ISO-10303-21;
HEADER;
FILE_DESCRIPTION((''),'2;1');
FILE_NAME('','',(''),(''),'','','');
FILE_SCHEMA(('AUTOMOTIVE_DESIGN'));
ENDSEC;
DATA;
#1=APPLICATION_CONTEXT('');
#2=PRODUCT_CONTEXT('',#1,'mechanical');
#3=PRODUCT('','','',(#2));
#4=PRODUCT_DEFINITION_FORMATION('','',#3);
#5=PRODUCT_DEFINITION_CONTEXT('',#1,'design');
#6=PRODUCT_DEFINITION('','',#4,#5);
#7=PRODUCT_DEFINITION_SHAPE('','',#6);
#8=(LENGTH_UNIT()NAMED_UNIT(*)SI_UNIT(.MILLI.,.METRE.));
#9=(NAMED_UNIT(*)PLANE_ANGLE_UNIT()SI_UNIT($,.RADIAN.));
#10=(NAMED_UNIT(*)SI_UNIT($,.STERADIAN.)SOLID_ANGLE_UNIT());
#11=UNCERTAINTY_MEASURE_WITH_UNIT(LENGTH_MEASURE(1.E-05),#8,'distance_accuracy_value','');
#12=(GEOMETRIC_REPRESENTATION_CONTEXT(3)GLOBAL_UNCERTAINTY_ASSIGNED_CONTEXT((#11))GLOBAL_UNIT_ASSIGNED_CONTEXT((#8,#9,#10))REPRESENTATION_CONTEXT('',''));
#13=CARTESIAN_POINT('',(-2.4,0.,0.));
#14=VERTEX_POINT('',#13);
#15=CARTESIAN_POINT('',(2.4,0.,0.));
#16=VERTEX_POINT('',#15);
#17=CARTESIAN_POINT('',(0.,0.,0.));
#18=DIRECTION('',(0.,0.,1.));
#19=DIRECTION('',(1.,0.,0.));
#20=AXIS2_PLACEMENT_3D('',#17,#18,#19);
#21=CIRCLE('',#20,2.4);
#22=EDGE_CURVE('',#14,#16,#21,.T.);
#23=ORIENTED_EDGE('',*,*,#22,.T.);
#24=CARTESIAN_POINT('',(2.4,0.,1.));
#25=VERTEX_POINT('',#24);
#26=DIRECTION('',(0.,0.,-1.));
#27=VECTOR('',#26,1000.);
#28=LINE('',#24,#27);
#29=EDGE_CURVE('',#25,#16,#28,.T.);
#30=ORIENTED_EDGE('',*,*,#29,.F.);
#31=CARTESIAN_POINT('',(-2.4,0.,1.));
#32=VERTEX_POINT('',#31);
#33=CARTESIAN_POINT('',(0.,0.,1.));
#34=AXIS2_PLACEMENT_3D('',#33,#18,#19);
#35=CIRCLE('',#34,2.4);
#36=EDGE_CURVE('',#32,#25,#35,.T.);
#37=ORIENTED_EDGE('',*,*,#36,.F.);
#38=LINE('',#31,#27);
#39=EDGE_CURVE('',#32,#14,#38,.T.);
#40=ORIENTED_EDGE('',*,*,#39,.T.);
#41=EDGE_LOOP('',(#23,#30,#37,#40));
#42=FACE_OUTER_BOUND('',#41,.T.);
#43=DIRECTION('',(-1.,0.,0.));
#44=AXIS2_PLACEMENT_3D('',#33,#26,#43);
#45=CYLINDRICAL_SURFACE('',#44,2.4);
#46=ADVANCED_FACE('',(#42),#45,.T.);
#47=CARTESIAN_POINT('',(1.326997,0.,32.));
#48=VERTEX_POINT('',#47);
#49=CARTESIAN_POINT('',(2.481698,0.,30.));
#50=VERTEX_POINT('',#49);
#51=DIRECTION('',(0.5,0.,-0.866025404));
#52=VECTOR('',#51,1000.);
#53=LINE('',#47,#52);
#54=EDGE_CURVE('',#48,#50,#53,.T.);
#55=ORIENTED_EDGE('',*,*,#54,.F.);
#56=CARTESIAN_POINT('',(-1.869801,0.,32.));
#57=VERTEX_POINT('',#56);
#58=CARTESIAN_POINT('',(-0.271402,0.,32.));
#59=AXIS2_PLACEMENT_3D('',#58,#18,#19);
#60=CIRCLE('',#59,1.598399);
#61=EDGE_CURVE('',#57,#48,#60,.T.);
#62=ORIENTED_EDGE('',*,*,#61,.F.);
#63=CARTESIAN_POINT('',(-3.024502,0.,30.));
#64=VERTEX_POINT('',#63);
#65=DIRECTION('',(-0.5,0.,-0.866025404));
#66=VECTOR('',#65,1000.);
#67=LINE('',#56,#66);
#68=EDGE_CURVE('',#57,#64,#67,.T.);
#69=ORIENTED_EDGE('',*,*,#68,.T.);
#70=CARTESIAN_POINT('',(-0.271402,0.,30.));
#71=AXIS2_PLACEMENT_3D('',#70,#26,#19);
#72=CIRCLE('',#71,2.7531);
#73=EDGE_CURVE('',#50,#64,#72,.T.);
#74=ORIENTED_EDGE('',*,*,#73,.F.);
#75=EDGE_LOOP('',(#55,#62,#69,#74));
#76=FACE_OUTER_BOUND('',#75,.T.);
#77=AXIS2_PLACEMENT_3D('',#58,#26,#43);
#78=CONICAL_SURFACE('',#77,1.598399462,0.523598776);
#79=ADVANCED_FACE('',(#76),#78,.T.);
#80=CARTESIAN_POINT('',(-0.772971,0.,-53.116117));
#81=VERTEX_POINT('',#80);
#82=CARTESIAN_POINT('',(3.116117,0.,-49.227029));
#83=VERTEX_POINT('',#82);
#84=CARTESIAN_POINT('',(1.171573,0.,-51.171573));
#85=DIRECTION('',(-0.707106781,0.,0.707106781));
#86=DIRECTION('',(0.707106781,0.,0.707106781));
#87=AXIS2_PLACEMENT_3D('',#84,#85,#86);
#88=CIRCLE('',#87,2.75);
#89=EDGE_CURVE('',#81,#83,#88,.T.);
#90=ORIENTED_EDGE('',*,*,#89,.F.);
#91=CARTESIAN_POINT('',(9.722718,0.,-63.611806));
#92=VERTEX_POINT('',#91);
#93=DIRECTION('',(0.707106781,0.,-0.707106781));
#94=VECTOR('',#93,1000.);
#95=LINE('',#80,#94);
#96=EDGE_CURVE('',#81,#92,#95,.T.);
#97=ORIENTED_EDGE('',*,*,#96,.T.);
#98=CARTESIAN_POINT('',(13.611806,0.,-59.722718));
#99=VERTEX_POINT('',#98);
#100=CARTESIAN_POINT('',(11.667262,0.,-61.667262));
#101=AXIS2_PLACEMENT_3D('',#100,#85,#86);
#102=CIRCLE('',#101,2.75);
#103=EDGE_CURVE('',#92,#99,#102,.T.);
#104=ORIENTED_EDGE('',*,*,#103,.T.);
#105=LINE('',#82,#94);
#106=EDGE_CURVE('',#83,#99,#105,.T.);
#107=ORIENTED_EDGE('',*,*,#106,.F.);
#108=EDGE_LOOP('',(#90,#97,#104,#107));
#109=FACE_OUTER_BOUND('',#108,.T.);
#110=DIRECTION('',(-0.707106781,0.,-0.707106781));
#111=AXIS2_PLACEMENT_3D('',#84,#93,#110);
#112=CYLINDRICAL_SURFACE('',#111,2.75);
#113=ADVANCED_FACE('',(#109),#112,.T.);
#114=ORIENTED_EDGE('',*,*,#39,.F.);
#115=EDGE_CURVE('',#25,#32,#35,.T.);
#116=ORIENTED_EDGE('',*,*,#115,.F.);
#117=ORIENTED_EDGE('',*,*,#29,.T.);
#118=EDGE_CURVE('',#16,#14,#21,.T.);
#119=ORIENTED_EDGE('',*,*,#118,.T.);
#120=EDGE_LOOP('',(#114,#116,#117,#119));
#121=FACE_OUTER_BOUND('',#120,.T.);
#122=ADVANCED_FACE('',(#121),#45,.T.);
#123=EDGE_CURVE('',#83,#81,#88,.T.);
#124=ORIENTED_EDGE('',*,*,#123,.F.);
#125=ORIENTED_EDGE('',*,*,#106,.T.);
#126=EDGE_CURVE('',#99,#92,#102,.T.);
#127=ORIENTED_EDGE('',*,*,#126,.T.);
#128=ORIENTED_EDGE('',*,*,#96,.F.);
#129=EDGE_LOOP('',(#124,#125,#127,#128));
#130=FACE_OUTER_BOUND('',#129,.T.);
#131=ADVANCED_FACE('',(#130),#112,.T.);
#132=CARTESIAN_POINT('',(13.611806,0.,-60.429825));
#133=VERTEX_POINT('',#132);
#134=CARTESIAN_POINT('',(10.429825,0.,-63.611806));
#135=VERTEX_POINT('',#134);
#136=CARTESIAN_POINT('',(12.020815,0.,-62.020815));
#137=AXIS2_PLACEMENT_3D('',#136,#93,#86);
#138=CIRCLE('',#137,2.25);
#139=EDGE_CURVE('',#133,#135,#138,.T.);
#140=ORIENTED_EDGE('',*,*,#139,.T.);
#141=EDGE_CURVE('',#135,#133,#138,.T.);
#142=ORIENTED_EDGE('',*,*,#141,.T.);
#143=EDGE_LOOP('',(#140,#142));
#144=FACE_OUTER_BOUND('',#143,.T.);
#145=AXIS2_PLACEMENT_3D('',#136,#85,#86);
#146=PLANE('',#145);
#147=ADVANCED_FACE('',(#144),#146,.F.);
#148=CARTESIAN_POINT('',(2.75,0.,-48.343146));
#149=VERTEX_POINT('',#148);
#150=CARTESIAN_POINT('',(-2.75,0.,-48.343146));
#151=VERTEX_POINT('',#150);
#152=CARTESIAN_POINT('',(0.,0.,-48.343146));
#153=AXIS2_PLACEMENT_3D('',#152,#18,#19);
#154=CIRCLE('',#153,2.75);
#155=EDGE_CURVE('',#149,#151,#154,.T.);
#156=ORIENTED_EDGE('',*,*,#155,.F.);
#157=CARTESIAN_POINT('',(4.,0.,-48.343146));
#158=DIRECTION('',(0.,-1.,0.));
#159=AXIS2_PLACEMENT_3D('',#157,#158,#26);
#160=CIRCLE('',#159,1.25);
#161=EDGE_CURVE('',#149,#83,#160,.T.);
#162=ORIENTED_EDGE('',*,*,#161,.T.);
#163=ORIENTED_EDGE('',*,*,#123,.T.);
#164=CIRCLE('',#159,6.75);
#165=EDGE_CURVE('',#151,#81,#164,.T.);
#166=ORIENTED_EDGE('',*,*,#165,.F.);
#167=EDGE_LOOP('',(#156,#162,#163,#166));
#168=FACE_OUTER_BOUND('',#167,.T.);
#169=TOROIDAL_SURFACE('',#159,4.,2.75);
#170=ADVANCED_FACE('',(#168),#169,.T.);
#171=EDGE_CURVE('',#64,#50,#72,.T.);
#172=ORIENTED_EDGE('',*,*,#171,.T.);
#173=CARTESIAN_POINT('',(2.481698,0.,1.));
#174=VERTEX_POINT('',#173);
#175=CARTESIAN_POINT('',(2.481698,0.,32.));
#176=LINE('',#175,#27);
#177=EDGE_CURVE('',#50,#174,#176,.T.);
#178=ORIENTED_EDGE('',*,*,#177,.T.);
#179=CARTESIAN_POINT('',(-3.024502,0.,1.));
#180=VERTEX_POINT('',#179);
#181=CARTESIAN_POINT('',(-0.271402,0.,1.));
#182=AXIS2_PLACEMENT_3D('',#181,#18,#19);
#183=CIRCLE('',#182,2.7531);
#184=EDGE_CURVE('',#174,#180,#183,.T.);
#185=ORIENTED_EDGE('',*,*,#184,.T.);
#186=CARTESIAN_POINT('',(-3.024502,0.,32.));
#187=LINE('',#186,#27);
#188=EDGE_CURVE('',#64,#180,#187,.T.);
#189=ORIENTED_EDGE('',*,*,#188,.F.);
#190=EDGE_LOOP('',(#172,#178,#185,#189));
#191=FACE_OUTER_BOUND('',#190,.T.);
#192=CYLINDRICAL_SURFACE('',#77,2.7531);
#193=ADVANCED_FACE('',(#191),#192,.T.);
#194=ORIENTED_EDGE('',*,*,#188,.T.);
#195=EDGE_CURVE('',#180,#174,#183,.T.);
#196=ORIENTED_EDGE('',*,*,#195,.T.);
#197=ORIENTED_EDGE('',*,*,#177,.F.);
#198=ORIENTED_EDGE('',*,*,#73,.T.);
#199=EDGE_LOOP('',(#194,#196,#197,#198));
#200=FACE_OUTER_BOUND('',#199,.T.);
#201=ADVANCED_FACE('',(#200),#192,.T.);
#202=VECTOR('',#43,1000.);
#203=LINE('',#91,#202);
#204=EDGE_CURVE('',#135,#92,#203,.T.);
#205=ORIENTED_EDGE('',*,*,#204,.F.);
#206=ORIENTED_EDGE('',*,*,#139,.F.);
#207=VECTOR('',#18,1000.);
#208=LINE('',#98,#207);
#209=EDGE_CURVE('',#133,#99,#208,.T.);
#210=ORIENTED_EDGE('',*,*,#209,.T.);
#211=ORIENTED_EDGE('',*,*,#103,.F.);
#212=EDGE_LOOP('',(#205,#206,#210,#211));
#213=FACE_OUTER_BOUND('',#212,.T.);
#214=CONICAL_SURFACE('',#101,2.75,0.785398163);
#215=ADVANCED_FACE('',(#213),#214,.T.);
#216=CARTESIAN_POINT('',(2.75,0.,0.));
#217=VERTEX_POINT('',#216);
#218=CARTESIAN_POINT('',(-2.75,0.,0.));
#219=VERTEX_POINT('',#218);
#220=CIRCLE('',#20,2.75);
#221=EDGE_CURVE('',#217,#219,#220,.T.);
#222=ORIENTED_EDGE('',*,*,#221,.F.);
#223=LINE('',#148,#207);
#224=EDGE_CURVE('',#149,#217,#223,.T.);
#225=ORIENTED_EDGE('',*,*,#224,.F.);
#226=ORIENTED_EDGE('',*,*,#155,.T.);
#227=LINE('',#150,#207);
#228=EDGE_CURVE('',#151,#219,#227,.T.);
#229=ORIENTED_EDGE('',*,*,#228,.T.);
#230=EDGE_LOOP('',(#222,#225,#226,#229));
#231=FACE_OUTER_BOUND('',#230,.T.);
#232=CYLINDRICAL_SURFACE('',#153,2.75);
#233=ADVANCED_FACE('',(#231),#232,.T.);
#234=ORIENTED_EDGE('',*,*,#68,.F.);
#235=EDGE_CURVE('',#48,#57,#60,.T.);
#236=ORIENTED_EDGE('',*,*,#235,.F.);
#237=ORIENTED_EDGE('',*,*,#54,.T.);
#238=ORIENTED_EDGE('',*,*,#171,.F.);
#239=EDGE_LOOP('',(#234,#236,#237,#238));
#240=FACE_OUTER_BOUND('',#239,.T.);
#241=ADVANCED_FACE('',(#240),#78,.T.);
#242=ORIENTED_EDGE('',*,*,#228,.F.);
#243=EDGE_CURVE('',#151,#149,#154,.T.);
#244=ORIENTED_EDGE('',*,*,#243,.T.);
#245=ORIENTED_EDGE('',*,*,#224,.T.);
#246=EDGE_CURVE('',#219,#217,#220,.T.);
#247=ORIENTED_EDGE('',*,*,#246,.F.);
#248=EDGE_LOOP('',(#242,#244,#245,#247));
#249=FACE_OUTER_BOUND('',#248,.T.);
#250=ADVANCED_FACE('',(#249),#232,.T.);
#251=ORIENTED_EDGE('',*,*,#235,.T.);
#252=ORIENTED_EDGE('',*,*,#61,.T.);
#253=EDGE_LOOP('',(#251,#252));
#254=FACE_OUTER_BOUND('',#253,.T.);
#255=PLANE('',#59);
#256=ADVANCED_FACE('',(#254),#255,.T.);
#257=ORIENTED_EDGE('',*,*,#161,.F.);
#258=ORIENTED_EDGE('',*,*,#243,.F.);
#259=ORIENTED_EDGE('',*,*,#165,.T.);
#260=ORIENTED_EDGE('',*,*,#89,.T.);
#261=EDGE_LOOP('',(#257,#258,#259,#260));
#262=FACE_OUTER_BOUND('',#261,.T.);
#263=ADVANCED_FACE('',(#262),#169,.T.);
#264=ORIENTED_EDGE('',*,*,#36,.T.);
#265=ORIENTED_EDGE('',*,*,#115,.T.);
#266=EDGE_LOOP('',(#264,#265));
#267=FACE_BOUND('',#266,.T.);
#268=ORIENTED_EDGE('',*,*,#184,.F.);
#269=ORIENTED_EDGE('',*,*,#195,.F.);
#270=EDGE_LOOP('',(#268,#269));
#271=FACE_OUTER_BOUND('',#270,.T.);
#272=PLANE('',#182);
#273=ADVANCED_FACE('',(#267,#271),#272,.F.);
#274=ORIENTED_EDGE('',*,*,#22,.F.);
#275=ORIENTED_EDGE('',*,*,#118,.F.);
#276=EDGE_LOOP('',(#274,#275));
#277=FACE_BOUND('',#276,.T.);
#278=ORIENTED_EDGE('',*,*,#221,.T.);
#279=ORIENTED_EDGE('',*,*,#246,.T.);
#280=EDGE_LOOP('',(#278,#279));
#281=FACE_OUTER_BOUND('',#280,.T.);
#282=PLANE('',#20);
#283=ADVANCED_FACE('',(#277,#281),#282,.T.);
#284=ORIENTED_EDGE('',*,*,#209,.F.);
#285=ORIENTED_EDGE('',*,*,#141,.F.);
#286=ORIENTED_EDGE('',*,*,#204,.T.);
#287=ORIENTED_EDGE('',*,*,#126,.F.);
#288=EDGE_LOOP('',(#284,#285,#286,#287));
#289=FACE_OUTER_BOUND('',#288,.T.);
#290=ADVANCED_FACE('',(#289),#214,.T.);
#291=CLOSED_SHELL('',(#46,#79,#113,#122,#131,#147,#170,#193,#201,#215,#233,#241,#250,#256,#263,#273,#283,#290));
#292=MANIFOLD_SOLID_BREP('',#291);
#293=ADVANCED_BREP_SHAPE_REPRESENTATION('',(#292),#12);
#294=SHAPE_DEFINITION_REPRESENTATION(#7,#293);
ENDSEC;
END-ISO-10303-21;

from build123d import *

# Parameters (mm, degrees)
SKETCH1_R           = 2.75
SKETCH4_R           = 2.4
BOSS_EXTRUDE1_DEPTH = 1
SKETCH5_R           = 2.7531
BOSS_EXTRUDE2_DEPTH = 31
CHAMFER2_SIZE       = 2
CHAMFER2_SIZE2      = 1.154700538
CHAMFER3_SIZE       = 0.5


with BuildPart() as part:
    # Sweep1: sweep along a path in Sketch2
    with BuildLine(Plane(origin=(0, 0, 0), x_dir=(1, 0, 0), z_dir=(0, 1, 0))) as sweep1_path:
        Line((0, 0), (0, 48.343145751))
        ThreePointArc((0, 48.343145751), (0.30448187, 49.87387948), (1.171572875, 51.171572875))
        Line((1.171572875, 51.171572875), (12.02081528, 62.02081528))
    # Sketch1 → Sweep1 (sweep)
    with BuildSketch(Plane.XY):
        Circle(SKETCH1_R)
    sweep(path=sweep1_path.line)

    # Sketch4 → Boss-Extrude1 (add)
    with BuildSketch(Plane.XY):
        Circle(SKETCH4_R)
    extrude(amount=BOSS_EXTRUDE1_DEPTH)

    # Sketch5 → Boss-Extrude2 (add)
    with BuildSketch(Plane.XY.offset(1)):
        with Locations((-0.271402, 0)):
            Circle(SKETCH5_R)
    extrude(amount=BOSS_EXTRUDE2_DEPTH)

    # Chamfer2
    chamfer2_edges = [part.edges().sort_by_distance(p)[0] for p in [
        (-3.024502, 0, 32),
    ]]
    chamfer2_side = [part.faces().sort_by_distance(p)[0] for p in [
        (-3.024502, 0, 16.5),
    ]]
    chamfer(chamfer2_edges, length=CHAMFER2_SIZE, length2=CHAMFER2_SIZE2, reference=chamfer2_side[0])

    # Chamfer3
    chamfer3_edges = [part.edges().sort_by_distance(p)[0] for p in [
        (10.076271632, 0, -63.965358928),
    ]]
    chamfer(chamfer3_edges, length=CHAMFER3_SIZE)


solid = part.part
